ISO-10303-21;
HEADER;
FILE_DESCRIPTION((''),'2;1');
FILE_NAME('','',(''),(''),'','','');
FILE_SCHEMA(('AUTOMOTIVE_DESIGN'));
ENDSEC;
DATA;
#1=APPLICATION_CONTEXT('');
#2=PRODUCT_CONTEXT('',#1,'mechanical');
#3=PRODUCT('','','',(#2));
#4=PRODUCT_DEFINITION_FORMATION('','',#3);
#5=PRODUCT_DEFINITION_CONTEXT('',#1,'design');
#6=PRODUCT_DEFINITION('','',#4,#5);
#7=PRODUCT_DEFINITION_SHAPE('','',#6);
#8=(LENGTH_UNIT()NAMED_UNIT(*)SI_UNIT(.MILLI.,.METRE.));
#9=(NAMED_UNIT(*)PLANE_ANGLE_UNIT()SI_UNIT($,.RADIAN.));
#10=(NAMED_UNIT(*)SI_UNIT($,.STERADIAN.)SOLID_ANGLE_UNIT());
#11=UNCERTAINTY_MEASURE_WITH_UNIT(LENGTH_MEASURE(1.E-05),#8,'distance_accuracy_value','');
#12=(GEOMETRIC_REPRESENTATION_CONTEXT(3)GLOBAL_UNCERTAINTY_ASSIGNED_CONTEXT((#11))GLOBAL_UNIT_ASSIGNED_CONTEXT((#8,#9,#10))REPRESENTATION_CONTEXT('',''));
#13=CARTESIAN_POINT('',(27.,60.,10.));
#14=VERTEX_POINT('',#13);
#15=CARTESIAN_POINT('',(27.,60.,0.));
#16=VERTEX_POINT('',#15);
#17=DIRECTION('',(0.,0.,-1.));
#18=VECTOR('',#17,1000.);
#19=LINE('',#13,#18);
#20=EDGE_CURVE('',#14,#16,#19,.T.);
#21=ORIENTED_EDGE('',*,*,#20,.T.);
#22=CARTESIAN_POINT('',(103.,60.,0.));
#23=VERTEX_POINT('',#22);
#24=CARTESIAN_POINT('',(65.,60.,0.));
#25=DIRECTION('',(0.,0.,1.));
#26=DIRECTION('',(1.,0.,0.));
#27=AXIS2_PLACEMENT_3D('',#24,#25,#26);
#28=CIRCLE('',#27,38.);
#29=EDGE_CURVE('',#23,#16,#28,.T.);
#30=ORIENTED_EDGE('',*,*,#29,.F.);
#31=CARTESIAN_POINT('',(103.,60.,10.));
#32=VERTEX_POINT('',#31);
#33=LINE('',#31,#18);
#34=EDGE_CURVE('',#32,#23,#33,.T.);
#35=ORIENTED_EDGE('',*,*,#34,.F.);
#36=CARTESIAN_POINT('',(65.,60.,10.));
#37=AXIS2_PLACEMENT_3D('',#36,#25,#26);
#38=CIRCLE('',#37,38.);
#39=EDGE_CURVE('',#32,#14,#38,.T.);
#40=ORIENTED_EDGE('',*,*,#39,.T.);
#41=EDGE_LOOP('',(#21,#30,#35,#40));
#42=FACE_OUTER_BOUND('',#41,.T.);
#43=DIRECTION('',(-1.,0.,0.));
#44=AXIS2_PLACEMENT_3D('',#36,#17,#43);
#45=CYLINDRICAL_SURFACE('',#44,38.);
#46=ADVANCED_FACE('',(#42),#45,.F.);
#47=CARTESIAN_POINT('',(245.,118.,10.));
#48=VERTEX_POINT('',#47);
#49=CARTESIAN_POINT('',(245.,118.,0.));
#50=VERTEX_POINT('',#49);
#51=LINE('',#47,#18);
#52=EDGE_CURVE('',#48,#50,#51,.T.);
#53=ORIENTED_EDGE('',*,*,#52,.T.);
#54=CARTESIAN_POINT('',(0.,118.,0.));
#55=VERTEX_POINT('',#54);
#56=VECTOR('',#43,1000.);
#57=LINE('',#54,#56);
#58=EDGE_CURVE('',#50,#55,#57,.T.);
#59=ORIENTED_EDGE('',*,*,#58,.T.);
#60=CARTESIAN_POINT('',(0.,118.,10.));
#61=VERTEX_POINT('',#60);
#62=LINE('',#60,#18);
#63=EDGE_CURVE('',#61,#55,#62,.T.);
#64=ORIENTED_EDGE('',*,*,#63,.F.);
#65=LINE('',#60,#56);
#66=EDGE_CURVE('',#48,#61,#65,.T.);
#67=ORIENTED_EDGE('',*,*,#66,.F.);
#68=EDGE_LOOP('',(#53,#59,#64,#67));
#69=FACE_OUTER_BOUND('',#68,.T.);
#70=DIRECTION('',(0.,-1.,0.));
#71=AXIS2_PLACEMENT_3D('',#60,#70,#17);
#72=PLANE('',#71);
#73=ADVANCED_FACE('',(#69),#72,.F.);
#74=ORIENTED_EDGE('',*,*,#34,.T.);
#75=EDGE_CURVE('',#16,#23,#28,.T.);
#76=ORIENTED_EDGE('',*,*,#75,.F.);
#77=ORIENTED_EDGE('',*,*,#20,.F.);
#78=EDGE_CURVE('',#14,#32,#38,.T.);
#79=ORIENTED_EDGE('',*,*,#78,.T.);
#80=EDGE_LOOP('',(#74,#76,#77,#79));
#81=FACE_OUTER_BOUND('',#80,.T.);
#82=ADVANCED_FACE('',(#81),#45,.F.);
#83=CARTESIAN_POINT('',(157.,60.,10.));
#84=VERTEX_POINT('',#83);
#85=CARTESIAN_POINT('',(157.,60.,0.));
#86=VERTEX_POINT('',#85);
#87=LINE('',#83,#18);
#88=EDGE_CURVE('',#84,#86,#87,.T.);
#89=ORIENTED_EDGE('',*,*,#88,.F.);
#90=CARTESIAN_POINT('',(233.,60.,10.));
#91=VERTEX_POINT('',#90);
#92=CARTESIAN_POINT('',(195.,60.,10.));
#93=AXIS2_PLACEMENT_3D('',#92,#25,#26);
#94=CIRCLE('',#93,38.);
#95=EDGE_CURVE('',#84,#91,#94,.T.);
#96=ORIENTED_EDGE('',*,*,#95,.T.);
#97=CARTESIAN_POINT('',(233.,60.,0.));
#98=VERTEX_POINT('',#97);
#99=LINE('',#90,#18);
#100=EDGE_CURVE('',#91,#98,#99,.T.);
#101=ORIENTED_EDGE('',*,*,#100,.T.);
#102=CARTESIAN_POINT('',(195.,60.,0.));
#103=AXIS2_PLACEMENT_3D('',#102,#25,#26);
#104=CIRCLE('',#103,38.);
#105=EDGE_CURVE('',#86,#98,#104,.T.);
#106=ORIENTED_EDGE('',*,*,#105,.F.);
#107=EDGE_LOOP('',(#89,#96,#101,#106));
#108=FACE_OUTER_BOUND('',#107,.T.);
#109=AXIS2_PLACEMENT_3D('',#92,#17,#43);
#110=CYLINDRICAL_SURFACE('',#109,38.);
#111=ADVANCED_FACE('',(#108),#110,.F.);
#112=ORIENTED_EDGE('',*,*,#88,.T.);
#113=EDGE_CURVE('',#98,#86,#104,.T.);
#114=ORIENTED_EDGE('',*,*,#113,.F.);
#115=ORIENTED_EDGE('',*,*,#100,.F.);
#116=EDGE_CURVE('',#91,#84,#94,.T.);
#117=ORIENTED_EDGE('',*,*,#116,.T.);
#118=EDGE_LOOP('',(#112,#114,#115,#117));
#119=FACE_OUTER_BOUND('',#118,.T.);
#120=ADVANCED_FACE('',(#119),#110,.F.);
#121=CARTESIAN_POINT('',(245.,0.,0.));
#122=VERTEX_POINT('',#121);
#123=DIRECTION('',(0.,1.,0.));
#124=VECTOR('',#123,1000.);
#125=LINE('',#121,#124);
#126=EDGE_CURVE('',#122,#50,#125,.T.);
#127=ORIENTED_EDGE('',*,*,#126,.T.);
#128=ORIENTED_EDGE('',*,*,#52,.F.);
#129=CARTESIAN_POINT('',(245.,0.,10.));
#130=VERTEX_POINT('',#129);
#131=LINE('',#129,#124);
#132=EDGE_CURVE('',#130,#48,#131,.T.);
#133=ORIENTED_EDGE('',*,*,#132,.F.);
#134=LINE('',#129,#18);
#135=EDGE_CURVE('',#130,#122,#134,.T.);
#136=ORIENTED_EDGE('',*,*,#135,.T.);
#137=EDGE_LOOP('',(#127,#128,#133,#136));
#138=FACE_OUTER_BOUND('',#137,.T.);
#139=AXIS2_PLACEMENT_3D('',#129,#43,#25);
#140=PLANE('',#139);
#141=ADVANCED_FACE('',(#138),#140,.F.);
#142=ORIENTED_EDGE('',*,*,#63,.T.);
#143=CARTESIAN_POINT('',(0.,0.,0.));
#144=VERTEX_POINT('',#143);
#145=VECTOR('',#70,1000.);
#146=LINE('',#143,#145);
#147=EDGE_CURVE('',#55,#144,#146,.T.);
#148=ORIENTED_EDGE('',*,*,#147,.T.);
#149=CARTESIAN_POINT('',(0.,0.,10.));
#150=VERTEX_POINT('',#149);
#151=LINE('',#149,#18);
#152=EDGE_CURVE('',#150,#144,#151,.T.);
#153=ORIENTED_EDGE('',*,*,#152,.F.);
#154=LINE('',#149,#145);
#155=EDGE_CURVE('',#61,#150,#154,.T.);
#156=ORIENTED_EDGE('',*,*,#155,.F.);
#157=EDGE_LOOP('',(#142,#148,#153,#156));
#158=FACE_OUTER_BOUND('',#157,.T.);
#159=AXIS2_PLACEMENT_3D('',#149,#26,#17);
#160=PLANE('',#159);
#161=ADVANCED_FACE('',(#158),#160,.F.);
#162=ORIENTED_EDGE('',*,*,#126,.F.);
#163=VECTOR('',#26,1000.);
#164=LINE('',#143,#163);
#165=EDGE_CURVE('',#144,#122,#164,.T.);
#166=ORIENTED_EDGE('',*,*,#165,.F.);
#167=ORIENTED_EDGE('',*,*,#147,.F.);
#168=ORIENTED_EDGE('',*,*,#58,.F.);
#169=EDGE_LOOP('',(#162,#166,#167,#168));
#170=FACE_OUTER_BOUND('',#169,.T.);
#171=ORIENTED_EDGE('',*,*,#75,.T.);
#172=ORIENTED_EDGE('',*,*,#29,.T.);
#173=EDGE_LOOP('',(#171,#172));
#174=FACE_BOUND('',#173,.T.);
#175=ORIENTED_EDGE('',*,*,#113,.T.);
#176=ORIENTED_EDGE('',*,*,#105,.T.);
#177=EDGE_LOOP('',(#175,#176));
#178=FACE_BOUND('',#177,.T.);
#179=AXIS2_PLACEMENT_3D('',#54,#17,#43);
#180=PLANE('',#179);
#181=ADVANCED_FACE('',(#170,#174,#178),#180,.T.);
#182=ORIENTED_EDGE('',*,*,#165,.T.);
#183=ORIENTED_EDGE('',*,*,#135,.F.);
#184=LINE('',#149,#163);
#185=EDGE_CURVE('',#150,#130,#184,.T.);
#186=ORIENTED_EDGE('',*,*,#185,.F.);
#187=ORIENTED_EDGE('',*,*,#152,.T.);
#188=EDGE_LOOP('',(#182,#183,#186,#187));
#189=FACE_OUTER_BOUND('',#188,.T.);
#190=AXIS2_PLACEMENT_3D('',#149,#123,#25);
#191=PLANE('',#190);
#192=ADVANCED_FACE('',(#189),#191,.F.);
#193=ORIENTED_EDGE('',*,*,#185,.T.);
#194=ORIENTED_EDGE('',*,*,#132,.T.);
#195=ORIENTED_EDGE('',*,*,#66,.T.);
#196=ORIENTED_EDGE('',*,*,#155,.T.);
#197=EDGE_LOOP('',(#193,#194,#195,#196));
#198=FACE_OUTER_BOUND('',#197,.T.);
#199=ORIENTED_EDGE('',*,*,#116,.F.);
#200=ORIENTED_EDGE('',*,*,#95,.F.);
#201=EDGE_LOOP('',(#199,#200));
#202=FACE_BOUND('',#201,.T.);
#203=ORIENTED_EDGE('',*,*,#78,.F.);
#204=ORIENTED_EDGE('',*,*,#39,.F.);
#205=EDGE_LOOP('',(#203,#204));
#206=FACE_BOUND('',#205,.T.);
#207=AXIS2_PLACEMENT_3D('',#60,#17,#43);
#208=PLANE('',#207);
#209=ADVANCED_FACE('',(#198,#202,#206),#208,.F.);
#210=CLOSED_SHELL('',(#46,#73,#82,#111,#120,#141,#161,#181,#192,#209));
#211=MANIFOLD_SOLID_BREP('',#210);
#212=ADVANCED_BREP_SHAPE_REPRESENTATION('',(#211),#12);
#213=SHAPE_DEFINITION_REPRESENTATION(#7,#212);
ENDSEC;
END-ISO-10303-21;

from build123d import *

# Parameters (mm, degrees)
SKETCH1_W           = 245
SKETCH1_H           = 118
SKETCH1_R           = 38
BOSS_EXTRUDE1_DEPTH = 10


with BuildPart() as part:
    # Sketch1 → Boss-Extrude1 (new body)
    with BuildSketch(Plane.XY):
        with Locations((122.5, 59)):
            Rectangle(SKETCH1_W, SKETCH1_H)
        with Locations((195, 60)):
            Circle(SKETCH1_R, mode=Mode.SUBTRACT)
        with Locations((65, 60)):
            Circle(SKETCH1_R, mode=Mode.SUBTRACT)
    extrude(amount=BOSS_EXTRUDE1_DEPTH)


solid = part.part
